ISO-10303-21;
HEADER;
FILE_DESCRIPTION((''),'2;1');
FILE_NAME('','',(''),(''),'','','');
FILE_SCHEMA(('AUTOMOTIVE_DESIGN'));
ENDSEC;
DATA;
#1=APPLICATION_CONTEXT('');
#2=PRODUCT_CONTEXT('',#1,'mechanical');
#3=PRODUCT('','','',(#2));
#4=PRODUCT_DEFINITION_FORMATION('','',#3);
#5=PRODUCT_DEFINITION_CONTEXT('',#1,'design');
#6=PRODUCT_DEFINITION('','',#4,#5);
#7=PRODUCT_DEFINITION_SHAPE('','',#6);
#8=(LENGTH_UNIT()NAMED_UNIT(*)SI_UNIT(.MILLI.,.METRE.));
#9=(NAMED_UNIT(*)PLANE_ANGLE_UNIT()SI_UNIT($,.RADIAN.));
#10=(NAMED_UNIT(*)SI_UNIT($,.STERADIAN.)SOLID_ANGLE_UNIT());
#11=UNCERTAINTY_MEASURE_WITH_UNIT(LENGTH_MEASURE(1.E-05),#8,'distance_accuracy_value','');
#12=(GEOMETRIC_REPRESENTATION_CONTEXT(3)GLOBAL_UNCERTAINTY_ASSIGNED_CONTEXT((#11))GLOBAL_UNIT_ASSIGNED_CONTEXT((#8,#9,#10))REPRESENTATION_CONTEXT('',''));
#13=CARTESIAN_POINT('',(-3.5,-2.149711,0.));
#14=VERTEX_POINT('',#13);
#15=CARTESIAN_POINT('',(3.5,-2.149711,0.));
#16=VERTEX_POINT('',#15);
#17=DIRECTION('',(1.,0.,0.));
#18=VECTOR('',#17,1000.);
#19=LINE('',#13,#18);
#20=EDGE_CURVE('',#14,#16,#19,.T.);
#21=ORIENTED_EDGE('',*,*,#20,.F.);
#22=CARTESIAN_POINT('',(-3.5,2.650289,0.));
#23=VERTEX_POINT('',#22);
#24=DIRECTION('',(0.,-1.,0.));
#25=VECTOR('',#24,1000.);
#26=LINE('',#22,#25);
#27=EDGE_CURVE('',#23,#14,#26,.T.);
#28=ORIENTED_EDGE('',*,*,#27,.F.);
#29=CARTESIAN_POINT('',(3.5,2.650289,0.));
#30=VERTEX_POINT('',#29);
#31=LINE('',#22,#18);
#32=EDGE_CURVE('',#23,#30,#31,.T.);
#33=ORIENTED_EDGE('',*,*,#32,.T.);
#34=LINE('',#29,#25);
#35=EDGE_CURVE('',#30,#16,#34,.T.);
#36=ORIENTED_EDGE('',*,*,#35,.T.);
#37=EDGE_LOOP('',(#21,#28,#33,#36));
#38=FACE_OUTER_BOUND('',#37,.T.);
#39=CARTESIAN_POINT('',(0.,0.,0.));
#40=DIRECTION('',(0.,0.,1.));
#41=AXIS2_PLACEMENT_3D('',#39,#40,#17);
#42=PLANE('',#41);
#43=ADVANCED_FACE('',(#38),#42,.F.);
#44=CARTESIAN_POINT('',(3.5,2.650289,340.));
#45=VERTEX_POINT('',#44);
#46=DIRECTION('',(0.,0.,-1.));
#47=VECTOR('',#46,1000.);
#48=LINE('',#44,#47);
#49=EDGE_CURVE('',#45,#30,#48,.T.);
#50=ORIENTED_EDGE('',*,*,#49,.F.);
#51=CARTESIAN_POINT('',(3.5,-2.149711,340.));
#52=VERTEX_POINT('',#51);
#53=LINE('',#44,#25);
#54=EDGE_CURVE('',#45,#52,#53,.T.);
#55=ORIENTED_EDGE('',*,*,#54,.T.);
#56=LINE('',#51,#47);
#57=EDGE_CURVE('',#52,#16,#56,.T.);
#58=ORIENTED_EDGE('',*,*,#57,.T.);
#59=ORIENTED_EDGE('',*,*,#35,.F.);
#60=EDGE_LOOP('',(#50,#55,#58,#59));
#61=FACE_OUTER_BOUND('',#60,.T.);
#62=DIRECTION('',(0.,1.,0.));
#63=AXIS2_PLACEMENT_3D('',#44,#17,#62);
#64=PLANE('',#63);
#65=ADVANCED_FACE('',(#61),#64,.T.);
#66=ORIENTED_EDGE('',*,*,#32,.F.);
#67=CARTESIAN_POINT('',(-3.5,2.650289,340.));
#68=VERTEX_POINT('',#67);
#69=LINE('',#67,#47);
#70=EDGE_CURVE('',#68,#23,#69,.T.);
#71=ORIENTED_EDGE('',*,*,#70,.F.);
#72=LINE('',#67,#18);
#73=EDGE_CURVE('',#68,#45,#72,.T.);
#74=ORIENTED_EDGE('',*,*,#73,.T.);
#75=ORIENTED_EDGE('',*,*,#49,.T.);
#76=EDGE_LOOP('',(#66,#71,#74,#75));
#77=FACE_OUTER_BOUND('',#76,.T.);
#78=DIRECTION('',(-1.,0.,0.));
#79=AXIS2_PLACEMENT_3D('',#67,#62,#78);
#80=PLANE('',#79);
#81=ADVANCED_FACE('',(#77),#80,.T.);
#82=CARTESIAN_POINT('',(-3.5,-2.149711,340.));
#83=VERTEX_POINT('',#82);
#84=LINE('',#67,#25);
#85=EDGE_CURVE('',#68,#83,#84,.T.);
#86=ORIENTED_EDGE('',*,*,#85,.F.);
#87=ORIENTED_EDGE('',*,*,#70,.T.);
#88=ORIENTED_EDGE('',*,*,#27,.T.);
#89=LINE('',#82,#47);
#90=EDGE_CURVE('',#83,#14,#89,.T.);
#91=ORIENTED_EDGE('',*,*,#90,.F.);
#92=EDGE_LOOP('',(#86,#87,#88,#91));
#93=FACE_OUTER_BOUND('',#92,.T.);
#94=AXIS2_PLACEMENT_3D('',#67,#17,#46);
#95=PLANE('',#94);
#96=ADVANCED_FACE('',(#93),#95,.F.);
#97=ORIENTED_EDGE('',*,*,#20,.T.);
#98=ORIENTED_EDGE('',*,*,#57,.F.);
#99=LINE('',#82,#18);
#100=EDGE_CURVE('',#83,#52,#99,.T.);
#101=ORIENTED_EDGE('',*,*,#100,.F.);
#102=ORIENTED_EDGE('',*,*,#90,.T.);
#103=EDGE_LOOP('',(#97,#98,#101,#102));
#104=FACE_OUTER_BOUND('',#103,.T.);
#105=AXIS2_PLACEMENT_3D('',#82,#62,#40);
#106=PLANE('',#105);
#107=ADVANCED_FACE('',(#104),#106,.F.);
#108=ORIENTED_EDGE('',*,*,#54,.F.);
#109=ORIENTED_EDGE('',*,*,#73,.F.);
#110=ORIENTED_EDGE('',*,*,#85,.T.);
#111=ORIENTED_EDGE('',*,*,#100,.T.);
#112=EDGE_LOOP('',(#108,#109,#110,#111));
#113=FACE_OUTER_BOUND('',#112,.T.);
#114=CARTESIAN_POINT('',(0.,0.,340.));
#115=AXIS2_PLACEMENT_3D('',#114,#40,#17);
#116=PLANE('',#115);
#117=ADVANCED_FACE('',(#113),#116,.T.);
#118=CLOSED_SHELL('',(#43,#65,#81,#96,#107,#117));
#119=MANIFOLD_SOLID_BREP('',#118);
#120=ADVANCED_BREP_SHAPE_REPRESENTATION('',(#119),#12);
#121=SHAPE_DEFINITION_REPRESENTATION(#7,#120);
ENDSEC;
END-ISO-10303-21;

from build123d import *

# Parameters (mm, degrees)
SKETCH1_W           = 7
SKETCH1_H           = 4.8
BOSS_EXTRUDE1_DEPTH = 340


with BuildPart() as part:
    # Sketch1 → Boss-Extrude1 (new body)
    with BuildSketch(Plane.XY):
        with Locations((0, 0.250289017)):
            Rectangle(SKETCH1_W, SKETCH1_H)
    extrude(amount=BOSS_EXTRUDE1_DEPTH)


solid = part.part
